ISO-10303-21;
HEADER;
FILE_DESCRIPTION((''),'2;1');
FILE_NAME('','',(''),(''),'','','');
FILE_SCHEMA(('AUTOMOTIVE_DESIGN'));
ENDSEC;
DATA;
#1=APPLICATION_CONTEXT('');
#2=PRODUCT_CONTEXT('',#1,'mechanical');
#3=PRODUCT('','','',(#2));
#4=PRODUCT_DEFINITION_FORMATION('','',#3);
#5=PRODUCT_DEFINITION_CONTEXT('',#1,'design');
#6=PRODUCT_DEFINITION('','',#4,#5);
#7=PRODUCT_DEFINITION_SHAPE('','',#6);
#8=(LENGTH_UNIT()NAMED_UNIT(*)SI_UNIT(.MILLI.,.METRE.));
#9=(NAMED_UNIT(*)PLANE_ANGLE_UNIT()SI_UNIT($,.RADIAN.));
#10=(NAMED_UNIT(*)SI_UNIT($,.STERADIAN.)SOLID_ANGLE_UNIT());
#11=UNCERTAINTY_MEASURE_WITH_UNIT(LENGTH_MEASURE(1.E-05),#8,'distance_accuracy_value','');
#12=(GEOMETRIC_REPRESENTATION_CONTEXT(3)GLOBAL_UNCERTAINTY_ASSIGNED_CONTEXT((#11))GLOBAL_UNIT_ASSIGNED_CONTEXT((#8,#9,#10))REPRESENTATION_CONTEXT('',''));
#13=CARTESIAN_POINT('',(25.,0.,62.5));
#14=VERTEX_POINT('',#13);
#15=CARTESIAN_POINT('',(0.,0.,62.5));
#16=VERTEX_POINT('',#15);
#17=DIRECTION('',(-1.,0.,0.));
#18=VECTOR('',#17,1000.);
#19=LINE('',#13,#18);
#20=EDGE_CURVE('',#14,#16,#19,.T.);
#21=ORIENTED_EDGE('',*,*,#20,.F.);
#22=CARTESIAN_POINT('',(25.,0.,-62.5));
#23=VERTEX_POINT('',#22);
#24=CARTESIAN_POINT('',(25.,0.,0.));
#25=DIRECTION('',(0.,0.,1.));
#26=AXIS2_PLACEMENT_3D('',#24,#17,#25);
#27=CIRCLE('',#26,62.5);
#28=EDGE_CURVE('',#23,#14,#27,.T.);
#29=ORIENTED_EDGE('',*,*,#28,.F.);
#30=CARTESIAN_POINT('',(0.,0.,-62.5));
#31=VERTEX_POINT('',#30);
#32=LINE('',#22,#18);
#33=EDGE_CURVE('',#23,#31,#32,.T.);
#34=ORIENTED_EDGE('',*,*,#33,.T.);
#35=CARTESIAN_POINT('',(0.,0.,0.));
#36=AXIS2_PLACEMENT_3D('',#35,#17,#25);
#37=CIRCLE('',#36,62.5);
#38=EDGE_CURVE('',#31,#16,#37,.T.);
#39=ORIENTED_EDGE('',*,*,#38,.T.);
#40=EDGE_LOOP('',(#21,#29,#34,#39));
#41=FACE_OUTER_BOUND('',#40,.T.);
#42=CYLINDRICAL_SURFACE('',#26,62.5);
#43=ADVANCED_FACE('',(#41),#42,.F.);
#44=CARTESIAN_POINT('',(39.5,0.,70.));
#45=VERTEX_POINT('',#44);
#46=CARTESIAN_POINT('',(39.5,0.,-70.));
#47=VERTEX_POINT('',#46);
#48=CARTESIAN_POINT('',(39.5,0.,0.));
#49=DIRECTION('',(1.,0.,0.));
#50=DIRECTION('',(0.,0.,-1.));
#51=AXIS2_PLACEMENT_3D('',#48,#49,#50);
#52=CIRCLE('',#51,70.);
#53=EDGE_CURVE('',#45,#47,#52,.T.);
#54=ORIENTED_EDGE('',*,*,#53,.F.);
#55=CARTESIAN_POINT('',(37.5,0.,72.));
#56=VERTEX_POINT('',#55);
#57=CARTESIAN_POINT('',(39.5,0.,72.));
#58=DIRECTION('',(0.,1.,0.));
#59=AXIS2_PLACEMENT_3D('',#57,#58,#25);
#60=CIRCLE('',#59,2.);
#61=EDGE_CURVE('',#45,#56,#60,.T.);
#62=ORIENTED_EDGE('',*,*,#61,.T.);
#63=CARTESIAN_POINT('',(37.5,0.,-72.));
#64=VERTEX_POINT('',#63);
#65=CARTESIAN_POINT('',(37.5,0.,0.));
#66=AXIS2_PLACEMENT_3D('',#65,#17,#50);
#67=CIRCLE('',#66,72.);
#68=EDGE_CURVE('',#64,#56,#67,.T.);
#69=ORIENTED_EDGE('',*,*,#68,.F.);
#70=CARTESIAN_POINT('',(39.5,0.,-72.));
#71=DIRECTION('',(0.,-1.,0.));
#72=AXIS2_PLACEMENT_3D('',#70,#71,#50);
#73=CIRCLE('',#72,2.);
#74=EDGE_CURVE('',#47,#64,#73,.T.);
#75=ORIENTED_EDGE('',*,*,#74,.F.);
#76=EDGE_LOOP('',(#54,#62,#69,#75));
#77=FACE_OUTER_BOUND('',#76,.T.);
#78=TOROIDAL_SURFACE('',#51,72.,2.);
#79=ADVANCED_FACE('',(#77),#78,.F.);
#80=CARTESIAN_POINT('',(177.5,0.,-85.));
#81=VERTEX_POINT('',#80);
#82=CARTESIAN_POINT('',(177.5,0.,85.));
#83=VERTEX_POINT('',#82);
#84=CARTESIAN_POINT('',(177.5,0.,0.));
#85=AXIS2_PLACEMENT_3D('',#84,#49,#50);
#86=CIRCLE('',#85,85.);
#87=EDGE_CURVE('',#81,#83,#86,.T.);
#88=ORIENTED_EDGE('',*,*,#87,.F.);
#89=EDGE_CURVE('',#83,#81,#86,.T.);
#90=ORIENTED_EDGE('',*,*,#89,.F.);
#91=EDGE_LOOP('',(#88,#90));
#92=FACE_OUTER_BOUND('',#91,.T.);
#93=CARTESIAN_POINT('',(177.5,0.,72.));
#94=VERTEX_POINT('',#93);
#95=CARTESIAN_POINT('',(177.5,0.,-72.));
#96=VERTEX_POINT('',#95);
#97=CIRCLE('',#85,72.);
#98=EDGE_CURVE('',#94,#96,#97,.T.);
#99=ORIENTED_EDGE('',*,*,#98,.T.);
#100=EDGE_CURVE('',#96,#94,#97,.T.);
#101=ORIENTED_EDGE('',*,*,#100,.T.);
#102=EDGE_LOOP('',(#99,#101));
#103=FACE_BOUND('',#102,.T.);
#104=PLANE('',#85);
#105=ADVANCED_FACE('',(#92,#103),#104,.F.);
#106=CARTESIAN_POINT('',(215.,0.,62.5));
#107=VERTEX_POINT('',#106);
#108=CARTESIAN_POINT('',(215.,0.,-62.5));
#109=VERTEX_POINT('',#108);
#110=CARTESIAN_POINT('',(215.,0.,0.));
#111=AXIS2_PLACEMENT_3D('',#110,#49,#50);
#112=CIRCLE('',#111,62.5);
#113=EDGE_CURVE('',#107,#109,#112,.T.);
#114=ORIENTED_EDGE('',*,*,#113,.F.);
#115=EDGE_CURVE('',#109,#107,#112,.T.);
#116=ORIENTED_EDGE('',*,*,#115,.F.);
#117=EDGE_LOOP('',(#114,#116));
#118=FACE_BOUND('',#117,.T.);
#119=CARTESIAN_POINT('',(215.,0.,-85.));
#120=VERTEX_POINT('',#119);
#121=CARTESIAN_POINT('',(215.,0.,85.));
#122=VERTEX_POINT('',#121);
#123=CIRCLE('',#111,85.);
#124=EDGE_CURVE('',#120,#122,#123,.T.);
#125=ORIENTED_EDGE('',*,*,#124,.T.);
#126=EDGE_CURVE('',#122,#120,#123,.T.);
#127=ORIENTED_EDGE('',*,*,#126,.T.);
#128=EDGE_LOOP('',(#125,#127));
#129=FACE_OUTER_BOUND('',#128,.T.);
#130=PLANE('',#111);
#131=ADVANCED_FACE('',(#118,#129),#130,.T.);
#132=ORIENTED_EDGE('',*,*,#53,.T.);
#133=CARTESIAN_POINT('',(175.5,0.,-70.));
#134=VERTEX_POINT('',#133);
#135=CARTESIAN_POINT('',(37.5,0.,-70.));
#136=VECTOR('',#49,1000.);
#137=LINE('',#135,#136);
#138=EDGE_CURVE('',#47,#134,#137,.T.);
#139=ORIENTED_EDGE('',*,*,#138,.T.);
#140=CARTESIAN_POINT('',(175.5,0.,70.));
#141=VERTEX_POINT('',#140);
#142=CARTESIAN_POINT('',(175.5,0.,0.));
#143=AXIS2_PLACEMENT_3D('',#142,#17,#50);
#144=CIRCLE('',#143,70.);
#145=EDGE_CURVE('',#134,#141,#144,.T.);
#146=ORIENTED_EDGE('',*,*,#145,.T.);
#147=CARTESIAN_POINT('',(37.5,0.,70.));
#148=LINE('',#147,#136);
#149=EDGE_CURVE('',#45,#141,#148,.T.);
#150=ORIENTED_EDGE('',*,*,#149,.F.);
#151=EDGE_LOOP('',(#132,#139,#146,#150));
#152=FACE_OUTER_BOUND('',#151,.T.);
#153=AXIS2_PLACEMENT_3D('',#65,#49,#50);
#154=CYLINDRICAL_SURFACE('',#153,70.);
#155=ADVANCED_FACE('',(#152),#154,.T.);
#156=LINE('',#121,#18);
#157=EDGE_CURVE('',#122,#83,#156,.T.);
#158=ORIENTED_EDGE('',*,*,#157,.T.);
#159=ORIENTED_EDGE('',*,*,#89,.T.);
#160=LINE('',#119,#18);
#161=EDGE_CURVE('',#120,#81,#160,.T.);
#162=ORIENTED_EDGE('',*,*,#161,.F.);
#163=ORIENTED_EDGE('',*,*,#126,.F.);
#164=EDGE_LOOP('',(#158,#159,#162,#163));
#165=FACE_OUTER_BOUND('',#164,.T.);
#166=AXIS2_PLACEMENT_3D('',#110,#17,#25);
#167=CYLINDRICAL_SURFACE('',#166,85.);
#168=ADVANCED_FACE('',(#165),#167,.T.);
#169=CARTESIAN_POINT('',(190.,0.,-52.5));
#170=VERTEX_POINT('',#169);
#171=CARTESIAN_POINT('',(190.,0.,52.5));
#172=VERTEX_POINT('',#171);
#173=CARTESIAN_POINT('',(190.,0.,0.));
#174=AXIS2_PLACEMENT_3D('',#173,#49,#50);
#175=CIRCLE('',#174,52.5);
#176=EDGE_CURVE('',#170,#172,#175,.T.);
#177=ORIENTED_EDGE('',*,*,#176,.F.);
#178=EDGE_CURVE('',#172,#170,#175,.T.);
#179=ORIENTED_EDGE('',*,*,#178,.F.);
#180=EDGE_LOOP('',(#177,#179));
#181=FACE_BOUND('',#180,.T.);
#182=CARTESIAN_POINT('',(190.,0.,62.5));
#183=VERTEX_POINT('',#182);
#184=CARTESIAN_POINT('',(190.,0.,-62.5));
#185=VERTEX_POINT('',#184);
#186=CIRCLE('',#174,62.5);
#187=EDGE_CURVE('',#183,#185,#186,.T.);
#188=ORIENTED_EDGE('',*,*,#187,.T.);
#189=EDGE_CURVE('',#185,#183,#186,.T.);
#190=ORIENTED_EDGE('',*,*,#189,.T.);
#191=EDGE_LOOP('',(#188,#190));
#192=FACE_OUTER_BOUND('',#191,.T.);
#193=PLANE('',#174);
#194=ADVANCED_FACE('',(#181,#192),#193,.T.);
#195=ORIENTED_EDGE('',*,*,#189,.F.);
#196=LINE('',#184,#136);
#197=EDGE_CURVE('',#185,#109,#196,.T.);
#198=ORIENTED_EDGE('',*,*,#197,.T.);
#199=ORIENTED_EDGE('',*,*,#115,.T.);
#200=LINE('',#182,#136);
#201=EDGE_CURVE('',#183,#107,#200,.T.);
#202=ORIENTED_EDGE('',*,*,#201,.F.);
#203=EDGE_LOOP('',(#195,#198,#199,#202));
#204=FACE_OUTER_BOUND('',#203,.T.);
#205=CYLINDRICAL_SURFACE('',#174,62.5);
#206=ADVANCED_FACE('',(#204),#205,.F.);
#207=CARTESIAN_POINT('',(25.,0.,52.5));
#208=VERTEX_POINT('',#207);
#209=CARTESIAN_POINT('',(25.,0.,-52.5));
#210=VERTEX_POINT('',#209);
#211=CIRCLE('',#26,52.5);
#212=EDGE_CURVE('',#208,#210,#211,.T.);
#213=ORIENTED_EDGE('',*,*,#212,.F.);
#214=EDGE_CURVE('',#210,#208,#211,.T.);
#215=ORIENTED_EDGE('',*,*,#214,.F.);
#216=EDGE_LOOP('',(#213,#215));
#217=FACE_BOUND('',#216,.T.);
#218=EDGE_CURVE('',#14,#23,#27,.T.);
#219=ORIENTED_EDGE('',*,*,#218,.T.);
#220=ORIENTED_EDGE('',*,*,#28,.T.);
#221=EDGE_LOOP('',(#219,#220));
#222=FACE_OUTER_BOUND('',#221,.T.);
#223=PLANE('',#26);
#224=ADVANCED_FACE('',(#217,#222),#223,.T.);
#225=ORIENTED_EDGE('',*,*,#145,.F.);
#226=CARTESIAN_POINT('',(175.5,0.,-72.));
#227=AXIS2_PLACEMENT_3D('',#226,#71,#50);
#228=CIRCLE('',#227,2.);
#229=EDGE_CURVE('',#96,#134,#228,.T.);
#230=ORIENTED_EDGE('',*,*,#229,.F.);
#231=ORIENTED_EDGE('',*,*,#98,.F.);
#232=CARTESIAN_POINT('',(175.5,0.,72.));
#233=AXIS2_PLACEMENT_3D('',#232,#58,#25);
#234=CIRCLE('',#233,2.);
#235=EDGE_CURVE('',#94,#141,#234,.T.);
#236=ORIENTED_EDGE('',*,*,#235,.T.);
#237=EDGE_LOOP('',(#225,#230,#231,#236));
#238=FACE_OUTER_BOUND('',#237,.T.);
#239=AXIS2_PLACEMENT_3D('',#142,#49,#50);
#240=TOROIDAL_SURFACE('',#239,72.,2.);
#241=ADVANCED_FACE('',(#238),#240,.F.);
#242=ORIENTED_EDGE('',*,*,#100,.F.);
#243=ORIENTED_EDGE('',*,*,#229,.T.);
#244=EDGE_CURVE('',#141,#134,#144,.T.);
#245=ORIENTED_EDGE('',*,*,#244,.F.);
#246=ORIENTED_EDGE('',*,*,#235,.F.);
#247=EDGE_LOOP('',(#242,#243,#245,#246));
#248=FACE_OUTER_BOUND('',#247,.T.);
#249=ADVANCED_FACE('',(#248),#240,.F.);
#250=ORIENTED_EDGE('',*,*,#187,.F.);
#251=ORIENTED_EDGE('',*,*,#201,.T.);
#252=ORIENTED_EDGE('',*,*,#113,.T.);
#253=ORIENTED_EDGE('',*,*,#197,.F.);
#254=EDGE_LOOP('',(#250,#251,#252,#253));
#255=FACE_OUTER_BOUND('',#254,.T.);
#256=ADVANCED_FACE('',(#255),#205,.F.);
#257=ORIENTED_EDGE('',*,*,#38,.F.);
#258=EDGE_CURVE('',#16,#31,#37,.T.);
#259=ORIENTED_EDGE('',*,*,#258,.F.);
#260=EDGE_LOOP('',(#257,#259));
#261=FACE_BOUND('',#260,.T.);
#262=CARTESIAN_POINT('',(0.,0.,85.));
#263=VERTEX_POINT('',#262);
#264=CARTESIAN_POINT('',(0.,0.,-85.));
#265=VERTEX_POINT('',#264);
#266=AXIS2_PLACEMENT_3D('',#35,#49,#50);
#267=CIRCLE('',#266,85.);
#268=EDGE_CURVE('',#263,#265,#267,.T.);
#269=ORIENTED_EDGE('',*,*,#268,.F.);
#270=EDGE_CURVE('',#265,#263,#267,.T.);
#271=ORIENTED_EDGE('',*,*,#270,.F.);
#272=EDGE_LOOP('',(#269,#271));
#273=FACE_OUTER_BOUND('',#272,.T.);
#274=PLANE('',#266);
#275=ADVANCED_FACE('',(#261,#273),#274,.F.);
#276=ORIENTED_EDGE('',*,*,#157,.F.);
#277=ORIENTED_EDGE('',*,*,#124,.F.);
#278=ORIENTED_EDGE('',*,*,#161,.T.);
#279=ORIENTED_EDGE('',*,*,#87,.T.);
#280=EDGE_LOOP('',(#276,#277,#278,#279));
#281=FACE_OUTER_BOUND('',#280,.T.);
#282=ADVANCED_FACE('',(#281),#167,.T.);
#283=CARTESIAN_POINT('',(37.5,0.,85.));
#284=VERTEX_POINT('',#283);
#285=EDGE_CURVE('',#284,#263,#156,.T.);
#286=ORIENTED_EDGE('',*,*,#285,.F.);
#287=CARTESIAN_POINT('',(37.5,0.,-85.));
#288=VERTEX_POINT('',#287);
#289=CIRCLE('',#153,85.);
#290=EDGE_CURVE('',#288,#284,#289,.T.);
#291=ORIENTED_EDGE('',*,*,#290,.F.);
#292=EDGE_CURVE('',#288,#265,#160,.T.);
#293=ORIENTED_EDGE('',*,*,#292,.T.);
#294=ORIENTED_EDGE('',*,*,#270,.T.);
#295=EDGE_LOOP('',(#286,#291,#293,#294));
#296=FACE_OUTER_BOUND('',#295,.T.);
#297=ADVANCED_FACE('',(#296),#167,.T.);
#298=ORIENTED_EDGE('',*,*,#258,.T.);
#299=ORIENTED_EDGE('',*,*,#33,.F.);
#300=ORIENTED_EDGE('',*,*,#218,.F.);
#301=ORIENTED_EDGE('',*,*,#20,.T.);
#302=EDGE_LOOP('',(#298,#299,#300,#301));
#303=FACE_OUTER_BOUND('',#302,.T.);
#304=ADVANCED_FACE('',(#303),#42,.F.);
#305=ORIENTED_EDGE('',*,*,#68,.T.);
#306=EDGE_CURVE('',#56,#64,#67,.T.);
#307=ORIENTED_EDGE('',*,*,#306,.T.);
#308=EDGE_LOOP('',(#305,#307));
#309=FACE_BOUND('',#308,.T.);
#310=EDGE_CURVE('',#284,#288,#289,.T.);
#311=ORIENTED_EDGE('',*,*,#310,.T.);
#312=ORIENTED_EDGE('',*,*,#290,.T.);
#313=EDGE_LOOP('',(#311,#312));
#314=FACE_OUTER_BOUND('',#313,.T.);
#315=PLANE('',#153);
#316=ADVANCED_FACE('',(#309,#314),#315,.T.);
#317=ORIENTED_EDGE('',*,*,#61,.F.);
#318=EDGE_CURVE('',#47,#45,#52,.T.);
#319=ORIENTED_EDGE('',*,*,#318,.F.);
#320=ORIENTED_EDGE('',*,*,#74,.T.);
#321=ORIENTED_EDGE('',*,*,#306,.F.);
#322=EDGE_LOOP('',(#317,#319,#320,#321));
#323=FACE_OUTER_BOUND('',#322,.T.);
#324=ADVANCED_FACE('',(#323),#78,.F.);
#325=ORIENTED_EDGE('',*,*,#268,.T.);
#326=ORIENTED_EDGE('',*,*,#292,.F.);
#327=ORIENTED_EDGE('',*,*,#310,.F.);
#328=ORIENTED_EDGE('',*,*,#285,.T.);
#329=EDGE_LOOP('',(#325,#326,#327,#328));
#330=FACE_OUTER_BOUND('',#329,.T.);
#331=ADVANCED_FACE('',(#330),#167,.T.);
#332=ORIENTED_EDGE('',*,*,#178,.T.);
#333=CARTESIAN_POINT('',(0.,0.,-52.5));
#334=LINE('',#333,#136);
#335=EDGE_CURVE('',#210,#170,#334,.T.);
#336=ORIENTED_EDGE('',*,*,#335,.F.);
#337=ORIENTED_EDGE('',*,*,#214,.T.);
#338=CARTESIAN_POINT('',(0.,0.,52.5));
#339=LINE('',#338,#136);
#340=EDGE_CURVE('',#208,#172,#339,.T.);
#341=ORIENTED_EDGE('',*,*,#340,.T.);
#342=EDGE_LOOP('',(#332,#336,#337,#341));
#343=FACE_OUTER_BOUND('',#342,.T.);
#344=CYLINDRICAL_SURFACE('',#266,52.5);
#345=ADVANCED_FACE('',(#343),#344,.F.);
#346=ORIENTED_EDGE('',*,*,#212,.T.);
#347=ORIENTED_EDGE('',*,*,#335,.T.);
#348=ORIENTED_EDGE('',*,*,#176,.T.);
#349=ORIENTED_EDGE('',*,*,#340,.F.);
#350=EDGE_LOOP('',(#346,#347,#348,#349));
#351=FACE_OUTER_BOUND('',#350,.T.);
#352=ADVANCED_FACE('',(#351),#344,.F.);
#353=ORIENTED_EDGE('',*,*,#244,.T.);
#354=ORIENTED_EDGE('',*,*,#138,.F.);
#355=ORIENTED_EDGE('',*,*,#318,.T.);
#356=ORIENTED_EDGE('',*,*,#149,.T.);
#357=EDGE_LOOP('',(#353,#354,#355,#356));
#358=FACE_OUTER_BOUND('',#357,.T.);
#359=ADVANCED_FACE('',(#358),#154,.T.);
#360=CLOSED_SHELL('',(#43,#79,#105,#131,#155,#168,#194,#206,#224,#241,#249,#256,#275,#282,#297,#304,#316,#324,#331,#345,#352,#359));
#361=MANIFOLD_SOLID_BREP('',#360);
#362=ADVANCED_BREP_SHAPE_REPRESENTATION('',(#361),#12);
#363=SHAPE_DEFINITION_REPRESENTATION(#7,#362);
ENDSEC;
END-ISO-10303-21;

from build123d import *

# Parameters (mm, degrees)
SKETCH1_R           = 85
BOSS_EXTRUDE1_DEPTH = 215
CUT_EXTRUDE1_START  = 5
SKETCH2_R           = 110
SKETCH2_R_2         = 70
CUT_EXTRUDE1_DEPTH  = 140
FILLET1_R           = 2
SKETCH3_R           = 62.5
CUT_EXTRUDE2_DEPTH  = 25
CUT_EXTRUDE3_START  = -25
SKETCH4_R           = 62.5
CUT_EXTRUDE3_DEPTH  = 25
SKETCH5_R           = 52.5
CUT_EXTRUDE4_DEPTH  = 225.833271559


with BuildPart() as part:
    # Sketch1 → Boss-Extrude1 (new body)
    with BuildSketch(Plane(origin=(0, 0, 0), x_dir=(0, 0, -1), z_dir=(1, 0, 0))):
        Circle(SKETCH1_R)
    extrude(amount=BOSS_EXTRUDE1_DEPTH)

    # Sketch2 → Cut-Extrude1 (cut)
    with BuildSketch(Plane(origin=(172.5, 0, 0), x_dir=(0, 0, -1), z_dir=(1, 0, 0)).offset(CUT_EXTRUDE1_START)):
        Circle(SKETCH2_R)
        Circle(SKETCH2_R_2, mode=Mode.SUBTRACT)
    extrude(amount=-CUT_EXTRUDE1_DEPTH, mode=Mode.SUBTRACT)

    # Fillet1
    fillet1_edges = [part.edges().sort_by_distance(p)[0] for p in [
        (37.5, 0, 70),
        (177.5, 0, 70),
    ]]
    fillet(fillet1_edges, radius=FILLET1_R)

    # Sketch3 → Cut-Extrude2 (cut)
    with BuildSketch(Plane(origin=(215, 0, 0), x_dir=(0, 0, -1), z_dir=(1, 0, 0))):
        Circle(SKETCH3_R)
    extrude(amount=-CUT_EXTRUDE2_DEPTH, mode=Mode.SUBTRACT)

    # Sketch4 → Cut-Extrude3 (cut)
    with BuildSketch(Plane.ZY.offset(CUT_EXTRUDE3_START)):
        with Locations(Location((0, 0, 0), (0, 0, 180))):
            Circle(SKETCH4_R)
    extrude(amount=CUT_EXTRUDE3_DEPTH, mode=Mode.SUBTRACT)

    # Sketch5 → Cut-Extrude4 (cut, through all)
    with BuildSketch(Plane(origin=(190, 0, 0), x_dir=(0, 0, -1), z_dir=(1, 0, 0))):
        Circle(SKETCH5_R)
    extrude(amount=-CUT_EXTRUDE4_DEPTH, mode=Mode.SUBTRACT)


solid = part.part
